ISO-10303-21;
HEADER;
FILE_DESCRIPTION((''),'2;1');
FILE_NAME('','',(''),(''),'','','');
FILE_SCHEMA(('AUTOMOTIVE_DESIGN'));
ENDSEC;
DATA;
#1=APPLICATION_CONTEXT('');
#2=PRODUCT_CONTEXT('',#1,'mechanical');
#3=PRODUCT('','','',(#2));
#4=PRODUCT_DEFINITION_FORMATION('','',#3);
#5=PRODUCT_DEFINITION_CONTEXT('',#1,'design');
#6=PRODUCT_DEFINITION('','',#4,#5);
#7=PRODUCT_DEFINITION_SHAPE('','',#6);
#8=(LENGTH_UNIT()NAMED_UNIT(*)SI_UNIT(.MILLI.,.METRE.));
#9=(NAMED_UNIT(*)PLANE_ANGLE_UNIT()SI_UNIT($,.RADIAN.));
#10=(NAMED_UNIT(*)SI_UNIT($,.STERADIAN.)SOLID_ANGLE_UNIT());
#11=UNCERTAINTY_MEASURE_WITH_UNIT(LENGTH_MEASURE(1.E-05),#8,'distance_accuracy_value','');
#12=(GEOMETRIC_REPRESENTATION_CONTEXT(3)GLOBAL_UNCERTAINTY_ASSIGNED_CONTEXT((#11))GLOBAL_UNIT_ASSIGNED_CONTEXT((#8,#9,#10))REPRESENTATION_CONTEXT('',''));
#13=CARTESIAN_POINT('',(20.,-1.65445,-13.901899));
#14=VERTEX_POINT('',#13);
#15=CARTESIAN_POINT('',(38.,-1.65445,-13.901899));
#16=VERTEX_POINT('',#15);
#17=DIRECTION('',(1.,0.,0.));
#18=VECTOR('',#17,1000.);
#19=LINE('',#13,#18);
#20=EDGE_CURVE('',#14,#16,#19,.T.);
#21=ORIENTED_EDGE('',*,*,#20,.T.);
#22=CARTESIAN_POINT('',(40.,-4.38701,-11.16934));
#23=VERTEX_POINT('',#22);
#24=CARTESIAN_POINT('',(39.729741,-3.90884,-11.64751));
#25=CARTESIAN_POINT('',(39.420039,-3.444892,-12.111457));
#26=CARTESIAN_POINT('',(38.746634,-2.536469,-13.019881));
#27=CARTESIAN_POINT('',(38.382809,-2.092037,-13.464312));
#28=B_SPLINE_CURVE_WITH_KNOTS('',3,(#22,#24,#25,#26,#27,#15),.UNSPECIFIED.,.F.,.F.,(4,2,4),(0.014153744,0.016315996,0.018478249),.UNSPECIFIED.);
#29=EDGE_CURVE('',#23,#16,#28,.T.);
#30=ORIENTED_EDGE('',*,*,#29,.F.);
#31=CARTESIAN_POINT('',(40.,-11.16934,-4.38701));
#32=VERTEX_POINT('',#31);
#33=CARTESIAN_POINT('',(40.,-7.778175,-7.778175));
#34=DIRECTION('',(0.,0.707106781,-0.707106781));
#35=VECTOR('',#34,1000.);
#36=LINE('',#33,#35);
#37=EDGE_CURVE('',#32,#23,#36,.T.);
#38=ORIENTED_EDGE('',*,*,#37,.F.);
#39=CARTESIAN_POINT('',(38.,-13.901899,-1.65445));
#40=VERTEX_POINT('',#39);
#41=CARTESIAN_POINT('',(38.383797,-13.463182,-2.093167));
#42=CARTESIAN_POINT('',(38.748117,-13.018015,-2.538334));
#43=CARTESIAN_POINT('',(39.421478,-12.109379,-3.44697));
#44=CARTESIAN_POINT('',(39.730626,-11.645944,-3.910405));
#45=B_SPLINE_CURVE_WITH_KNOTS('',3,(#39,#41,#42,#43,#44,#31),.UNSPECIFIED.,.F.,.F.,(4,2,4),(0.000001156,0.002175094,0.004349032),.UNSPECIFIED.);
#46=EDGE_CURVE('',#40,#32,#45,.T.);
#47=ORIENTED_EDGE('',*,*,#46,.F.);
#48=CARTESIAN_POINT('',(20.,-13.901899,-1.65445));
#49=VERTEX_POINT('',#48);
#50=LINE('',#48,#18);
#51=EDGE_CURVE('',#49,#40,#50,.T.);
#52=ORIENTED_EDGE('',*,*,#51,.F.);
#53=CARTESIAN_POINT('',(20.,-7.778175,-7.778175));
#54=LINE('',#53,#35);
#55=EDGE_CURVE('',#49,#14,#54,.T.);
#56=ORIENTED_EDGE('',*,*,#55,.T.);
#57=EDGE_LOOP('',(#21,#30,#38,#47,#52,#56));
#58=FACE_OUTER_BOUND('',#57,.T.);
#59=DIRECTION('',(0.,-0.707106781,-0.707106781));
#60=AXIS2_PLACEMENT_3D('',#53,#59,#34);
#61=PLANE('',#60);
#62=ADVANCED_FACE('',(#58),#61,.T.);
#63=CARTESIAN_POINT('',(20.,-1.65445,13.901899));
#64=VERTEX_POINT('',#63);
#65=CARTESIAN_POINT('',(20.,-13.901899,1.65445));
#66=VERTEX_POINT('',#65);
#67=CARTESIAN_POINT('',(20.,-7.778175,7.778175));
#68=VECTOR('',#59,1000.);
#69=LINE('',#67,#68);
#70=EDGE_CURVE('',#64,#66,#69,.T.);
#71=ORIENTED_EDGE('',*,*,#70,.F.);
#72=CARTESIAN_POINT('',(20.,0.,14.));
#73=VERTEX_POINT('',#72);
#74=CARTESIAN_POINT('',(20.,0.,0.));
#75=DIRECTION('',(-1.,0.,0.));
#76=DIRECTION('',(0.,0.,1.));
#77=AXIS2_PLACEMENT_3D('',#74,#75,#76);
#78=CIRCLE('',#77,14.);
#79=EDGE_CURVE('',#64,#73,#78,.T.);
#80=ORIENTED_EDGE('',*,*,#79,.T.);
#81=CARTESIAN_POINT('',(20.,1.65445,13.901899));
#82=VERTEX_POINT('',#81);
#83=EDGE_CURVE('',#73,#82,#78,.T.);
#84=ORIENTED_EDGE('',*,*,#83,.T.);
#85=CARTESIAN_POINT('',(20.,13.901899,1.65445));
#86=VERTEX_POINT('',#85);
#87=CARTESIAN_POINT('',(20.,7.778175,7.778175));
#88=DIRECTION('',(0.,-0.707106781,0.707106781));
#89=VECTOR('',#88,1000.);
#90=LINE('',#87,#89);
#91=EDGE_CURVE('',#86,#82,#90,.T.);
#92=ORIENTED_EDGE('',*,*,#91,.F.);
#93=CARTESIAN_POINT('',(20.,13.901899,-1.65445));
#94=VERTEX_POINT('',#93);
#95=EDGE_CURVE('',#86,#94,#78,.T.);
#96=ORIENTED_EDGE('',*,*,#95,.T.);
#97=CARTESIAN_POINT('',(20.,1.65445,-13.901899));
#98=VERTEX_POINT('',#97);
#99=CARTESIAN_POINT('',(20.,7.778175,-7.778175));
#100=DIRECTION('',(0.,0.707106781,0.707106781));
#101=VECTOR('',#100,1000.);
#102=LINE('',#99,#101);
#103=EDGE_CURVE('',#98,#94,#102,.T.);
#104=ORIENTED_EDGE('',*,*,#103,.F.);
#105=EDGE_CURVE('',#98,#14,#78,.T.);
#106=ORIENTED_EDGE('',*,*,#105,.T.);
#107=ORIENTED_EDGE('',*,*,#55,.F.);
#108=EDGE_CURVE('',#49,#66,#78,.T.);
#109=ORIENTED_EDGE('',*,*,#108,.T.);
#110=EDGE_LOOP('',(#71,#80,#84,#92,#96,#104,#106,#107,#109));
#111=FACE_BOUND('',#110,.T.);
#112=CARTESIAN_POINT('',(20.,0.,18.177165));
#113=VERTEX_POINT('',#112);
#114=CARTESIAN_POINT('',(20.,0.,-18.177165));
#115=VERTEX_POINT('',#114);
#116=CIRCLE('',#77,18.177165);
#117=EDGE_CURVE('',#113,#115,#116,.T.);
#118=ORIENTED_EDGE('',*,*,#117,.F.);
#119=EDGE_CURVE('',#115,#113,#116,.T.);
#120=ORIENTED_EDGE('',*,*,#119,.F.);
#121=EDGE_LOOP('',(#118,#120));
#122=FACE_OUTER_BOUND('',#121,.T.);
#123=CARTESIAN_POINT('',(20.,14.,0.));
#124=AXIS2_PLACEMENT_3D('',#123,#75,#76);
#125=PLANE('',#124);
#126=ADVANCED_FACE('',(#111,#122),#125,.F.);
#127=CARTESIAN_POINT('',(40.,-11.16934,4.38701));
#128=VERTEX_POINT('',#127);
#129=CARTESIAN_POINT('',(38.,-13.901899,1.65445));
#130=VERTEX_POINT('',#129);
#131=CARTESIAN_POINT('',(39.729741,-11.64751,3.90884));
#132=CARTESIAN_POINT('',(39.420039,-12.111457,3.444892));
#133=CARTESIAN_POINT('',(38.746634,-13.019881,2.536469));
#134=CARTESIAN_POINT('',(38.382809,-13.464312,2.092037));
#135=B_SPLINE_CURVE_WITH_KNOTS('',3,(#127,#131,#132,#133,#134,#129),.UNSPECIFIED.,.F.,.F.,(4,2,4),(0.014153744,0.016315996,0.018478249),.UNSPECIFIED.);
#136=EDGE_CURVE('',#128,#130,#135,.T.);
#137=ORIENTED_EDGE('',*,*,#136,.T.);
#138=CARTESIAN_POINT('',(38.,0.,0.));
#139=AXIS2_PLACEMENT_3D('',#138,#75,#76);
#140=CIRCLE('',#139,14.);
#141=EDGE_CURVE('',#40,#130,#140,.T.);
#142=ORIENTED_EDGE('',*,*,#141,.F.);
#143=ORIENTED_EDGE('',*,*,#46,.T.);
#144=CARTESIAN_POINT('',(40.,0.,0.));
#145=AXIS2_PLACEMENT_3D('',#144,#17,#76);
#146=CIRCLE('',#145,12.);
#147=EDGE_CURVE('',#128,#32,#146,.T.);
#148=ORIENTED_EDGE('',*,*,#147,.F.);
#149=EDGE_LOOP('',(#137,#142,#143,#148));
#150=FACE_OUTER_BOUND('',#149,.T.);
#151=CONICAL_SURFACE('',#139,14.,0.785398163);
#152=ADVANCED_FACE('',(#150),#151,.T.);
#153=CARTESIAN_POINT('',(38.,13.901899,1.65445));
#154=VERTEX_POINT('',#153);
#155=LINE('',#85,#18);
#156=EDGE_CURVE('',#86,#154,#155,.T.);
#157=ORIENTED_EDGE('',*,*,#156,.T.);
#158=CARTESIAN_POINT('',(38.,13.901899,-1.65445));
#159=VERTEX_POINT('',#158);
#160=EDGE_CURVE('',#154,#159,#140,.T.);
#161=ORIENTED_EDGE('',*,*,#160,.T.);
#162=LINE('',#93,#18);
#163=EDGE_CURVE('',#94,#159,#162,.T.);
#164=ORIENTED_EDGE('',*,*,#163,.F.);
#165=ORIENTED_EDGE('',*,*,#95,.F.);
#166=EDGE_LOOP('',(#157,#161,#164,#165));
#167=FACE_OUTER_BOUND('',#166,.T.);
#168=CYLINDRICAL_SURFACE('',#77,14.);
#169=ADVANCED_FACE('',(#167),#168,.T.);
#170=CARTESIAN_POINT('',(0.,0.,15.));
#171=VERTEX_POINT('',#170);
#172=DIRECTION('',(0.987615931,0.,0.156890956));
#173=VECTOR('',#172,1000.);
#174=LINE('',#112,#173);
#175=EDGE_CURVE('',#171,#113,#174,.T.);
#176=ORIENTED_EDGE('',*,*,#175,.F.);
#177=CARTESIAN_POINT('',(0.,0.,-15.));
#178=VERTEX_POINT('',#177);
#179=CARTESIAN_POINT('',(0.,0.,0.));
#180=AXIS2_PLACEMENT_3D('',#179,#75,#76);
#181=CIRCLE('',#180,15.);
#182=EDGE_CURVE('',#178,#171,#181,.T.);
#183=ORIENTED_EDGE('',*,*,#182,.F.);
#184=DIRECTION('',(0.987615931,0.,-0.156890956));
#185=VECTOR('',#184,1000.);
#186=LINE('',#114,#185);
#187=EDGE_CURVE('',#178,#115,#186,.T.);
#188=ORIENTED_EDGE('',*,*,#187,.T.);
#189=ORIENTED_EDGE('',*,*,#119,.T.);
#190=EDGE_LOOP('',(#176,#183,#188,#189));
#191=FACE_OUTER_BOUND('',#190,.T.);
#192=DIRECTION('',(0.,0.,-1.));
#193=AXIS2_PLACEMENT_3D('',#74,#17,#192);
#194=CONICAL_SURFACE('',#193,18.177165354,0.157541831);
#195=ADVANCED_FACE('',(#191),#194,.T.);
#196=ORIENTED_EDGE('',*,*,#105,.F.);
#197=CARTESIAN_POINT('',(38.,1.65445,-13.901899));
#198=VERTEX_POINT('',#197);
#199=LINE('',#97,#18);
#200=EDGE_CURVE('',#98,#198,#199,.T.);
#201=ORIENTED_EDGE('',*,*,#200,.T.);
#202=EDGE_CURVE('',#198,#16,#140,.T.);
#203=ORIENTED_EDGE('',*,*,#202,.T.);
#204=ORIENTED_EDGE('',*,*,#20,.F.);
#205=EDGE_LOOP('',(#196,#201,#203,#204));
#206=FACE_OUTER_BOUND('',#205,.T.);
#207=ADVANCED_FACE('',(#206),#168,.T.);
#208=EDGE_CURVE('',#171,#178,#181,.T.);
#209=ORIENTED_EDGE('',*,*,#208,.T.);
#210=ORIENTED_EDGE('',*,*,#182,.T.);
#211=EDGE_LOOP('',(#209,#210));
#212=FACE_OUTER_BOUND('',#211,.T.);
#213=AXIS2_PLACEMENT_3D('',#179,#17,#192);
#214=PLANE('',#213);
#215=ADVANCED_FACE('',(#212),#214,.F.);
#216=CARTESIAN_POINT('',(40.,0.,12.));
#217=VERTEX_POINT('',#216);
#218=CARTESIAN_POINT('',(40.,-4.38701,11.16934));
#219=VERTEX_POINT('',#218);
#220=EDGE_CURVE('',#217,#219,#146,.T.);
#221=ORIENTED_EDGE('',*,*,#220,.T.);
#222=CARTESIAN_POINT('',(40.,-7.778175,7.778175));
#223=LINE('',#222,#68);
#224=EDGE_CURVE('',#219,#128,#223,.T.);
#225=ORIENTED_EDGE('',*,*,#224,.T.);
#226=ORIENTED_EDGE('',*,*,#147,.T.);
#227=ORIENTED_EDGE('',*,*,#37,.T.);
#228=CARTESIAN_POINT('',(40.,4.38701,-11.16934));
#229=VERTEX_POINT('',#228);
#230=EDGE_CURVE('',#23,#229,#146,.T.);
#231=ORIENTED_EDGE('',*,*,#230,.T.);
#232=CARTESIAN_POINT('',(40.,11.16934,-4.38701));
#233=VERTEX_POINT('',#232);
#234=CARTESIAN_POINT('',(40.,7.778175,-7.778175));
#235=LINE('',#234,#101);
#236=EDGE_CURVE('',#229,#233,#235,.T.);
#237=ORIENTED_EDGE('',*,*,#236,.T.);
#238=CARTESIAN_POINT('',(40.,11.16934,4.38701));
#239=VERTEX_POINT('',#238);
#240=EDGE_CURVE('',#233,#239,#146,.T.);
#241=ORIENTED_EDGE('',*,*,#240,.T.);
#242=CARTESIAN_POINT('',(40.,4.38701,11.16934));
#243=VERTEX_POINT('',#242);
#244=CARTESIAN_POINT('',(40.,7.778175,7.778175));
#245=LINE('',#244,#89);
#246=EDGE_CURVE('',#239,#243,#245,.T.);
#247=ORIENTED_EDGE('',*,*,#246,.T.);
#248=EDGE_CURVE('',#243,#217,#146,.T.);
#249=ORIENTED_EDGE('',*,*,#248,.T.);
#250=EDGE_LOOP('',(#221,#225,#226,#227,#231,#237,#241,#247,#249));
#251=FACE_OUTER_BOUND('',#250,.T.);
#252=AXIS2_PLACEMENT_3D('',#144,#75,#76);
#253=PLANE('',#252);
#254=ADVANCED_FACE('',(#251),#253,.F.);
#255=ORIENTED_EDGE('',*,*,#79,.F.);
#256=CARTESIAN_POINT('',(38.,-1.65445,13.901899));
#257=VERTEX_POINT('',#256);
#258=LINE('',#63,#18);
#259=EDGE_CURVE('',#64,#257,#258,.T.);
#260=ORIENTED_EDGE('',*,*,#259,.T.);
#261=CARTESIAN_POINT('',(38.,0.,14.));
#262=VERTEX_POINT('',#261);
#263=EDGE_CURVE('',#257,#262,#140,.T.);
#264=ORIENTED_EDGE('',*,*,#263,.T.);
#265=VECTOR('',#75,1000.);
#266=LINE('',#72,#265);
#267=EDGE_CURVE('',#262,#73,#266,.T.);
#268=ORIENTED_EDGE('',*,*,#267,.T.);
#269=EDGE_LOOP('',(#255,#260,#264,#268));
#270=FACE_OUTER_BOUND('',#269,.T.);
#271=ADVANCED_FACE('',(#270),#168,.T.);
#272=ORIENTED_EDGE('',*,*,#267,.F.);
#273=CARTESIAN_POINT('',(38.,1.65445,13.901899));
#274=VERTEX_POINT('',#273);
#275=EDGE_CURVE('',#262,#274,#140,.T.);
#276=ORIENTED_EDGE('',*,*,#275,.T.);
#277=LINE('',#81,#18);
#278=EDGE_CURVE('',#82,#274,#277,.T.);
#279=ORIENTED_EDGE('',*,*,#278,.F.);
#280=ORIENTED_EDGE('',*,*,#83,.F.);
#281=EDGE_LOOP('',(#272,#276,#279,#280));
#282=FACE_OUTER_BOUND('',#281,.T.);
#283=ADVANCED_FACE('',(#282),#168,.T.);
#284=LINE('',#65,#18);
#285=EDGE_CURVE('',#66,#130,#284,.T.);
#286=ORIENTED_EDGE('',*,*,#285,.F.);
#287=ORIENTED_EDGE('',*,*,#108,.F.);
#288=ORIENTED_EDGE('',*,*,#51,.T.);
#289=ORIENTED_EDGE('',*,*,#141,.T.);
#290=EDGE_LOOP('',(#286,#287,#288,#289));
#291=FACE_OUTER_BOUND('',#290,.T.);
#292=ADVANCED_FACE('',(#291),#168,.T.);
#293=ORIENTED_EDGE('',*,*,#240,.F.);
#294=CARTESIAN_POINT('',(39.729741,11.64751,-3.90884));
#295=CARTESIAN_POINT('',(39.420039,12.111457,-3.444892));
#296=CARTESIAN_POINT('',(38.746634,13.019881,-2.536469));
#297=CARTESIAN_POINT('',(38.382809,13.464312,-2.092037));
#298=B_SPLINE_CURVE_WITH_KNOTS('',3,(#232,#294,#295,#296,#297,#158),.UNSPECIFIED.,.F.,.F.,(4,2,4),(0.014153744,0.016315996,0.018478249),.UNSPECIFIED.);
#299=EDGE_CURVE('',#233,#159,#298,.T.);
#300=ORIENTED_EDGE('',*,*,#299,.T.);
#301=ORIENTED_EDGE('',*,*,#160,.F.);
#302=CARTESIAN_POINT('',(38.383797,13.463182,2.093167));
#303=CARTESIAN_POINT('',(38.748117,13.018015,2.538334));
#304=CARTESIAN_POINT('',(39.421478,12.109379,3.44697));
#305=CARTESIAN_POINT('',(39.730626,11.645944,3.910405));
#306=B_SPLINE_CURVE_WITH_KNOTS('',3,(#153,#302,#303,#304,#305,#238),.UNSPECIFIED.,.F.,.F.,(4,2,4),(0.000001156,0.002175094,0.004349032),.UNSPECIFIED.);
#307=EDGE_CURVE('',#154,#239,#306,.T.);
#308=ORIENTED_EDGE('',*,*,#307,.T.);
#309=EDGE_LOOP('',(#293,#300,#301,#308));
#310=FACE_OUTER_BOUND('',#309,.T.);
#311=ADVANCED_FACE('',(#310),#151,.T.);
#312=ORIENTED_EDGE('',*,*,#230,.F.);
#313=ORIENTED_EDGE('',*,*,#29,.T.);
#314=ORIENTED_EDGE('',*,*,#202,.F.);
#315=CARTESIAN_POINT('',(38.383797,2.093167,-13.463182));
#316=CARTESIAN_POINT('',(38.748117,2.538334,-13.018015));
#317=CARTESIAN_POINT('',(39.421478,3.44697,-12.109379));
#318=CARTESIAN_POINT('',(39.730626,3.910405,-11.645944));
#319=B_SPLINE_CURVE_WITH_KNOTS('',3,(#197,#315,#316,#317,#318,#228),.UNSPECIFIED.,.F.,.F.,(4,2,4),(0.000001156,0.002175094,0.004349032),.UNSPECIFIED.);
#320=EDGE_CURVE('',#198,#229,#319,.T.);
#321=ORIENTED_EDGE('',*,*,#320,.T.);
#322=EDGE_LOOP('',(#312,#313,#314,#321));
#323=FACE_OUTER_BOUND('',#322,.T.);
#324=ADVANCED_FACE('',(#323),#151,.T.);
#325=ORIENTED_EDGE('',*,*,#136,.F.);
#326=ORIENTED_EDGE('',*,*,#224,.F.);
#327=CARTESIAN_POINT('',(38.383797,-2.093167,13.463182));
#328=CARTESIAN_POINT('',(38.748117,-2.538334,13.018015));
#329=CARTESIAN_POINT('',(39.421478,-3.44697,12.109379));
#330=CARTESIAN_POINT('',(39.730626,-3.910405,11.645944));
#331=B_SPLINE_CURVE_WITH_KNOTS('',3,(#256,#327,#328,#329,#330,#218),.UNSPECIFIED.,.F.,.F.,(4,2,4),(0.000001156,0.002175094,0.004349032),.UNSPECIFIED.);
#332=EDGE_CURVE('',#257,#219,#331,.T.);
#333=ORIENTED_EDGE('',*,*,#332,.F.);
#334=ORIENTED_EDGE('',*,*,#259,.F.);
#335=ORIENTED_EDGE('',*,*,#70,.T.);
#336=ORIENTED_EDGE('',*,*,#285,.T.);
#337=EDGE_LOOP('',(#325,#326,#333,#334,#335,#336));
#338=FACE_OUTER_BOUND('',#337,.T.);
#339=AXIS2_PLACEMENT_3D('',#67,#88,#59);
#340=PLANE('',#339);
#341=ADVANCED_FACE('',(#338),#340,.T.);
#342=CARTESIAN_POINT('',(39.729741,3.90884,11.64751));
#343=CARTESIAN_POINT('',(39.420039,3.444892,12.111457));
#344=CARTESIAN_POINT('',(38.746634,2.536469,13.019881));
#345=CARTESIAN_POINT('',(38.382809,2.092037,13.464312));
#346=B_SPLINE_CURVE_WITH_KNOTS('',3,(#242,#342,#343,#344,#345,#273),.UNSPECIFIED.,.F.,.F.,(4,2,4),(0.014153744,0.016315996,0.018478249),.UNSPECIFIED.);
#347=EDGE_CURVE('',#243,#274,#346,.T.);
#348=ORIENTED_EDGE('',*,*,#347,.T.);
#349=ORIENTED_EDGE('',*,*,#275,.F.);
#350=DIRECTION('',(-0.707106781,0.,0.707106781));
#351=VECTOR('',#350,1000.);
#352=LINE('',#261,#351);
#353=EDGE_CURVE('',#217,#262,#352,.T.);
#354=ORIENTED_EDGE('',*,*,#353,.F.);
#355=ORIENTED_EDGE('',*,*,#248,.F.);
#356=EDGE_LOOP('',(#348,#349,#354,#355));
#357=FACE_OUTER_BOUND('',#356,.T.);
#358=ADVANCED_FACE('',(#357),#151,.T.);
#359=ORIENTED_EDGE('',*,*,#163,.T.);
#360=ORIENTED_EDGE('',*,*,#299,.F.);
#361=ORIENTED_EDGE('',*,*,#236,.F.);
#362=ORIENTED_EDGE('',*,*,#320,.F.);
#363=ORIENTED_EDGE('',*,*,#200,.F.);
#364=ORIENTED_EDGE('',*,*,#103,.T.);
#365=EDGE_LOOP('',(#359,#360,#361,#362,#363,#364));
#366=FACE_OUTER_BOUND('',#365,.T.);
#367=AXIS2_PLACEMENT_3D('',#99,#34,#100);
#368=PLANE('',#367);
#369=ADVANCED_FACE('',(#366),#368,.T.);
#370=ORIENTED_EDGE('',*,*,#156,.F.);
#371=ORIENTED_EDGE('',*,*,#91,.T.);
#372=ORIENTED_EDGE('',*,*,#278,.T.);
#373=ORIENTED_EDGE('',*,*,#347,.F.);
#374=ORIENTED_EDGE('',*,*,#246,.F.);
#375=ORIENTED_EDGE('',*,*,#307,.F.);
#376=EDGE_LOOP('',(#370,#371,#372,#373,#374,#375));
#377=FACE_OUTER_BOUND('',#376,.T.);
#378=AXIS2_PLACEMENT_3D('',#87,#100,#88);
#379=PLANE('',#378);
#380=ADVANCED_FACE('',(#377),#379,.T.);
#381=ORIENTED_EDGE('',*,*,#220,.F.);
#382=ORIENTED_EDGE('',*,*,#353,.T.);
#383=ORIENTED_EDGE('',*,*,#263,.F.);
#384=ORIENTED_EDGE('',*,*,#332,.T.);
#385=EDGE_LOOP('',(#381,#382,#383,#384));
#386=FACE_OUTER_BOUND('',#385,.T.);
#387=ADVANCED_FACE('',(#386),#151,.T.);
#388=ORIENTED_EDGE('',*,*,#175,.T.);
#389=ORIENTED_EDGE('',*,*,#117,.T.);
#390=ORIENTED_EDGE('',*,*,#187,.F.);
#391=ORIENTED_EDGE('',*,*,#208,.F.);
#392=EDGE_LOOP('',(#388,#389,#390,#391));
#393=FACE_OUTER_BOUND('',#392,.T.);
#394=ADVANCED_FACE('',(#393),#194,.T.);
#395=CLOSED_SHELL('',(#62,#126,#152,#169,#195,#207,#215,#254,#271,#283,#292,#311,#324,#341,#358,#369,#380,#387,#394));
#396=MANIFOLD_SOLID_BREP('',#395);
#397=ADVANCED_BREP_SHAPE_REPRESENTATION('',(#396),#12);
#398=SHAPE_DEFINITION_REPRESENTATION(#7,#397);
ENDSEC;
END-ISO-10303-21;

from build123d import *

# Parameters (mm, degrees)
CHAMFER1_SIZE      = 2
CUT_EXTRUDE1_START = -20
CUT_EXTRUDE1_DEPTH = 20
CIRPATTERN1_COUNT  = 4


with BuildPart() as part:
    # Sketch1 → Revolve1 (revolve)
    with BuildSketch(Plane.XY, mode=Mode.PRIVATE) as revolve1_sk:
        Polygon((0, 0), (20, 0), (40, 0), (40, 14), (20, 14), (20, 18.177165354), (0, 15), align=None)
    revolve(revolve1_sk.sketch.rotate(Axis((20, 0, 0), (1, 0, 0)), 90), axis=Axis((20, 0, 0), (1, 0, 0)))

    # Chamfer1
    chamfer1_edges = [part.edges().sort_by_distance(p)[0] for p in [
        (40, 0, -14),
    ]]
    chamfer(chamfer1_edges, length=CHAMFER1_SIZE)

    # Sketch2 → Cut-Extrude1 (cut)
    with BuildSketch(Plane(origin=(40, 0, 0), x_dir=(0, 0, -1), z_dir=(1, 0, 0)).offset(CUT_EXTRUDE1_START)):
        with BuildLine():
            Line((11.169339585, 4.387009601), (13.90189895, 1.654450236))
            ThreePointArc((13.90189895, 1.654450236), (9.899494937, 9.899494937), (1.654450236, 13.90189895))
            Line((1.654450236, 13.90189895), (4.387009601, 11.169339585))
            ThreePointArc((4.387009601, 11.169339585), (8.485281374, 8.485281374), (11.169339585, 4.387009601))
        make_face()
        with BuildLine():
            Line((4.387009601, 11.169339585), (11.169339585, 4.387009601))
            ThreePointArc((11.169339585, 4.387009601), (8.485281374, 8.485281374), (4.387009601, 11.169339585))
        make_face()
    cut_extrude1 = extrude(amount=CUT_EXTRUDE1_DEPTH, mode=Mode.SUBTRACT)

    # CirPattern1: Cut-Extrude1 ×4 about axis
    cirpattern1_axis = Axis((0, 0, 0), (1, 0, 0))
    for i in range(1, CIRPATTERN1_COUNT):
        add(cut_extrude1.rotate(cirpattern1_axis, i * 360 / CIRPATTERN1_COUNT), mode=Mode.SUBTRACT)


solid = part.part
